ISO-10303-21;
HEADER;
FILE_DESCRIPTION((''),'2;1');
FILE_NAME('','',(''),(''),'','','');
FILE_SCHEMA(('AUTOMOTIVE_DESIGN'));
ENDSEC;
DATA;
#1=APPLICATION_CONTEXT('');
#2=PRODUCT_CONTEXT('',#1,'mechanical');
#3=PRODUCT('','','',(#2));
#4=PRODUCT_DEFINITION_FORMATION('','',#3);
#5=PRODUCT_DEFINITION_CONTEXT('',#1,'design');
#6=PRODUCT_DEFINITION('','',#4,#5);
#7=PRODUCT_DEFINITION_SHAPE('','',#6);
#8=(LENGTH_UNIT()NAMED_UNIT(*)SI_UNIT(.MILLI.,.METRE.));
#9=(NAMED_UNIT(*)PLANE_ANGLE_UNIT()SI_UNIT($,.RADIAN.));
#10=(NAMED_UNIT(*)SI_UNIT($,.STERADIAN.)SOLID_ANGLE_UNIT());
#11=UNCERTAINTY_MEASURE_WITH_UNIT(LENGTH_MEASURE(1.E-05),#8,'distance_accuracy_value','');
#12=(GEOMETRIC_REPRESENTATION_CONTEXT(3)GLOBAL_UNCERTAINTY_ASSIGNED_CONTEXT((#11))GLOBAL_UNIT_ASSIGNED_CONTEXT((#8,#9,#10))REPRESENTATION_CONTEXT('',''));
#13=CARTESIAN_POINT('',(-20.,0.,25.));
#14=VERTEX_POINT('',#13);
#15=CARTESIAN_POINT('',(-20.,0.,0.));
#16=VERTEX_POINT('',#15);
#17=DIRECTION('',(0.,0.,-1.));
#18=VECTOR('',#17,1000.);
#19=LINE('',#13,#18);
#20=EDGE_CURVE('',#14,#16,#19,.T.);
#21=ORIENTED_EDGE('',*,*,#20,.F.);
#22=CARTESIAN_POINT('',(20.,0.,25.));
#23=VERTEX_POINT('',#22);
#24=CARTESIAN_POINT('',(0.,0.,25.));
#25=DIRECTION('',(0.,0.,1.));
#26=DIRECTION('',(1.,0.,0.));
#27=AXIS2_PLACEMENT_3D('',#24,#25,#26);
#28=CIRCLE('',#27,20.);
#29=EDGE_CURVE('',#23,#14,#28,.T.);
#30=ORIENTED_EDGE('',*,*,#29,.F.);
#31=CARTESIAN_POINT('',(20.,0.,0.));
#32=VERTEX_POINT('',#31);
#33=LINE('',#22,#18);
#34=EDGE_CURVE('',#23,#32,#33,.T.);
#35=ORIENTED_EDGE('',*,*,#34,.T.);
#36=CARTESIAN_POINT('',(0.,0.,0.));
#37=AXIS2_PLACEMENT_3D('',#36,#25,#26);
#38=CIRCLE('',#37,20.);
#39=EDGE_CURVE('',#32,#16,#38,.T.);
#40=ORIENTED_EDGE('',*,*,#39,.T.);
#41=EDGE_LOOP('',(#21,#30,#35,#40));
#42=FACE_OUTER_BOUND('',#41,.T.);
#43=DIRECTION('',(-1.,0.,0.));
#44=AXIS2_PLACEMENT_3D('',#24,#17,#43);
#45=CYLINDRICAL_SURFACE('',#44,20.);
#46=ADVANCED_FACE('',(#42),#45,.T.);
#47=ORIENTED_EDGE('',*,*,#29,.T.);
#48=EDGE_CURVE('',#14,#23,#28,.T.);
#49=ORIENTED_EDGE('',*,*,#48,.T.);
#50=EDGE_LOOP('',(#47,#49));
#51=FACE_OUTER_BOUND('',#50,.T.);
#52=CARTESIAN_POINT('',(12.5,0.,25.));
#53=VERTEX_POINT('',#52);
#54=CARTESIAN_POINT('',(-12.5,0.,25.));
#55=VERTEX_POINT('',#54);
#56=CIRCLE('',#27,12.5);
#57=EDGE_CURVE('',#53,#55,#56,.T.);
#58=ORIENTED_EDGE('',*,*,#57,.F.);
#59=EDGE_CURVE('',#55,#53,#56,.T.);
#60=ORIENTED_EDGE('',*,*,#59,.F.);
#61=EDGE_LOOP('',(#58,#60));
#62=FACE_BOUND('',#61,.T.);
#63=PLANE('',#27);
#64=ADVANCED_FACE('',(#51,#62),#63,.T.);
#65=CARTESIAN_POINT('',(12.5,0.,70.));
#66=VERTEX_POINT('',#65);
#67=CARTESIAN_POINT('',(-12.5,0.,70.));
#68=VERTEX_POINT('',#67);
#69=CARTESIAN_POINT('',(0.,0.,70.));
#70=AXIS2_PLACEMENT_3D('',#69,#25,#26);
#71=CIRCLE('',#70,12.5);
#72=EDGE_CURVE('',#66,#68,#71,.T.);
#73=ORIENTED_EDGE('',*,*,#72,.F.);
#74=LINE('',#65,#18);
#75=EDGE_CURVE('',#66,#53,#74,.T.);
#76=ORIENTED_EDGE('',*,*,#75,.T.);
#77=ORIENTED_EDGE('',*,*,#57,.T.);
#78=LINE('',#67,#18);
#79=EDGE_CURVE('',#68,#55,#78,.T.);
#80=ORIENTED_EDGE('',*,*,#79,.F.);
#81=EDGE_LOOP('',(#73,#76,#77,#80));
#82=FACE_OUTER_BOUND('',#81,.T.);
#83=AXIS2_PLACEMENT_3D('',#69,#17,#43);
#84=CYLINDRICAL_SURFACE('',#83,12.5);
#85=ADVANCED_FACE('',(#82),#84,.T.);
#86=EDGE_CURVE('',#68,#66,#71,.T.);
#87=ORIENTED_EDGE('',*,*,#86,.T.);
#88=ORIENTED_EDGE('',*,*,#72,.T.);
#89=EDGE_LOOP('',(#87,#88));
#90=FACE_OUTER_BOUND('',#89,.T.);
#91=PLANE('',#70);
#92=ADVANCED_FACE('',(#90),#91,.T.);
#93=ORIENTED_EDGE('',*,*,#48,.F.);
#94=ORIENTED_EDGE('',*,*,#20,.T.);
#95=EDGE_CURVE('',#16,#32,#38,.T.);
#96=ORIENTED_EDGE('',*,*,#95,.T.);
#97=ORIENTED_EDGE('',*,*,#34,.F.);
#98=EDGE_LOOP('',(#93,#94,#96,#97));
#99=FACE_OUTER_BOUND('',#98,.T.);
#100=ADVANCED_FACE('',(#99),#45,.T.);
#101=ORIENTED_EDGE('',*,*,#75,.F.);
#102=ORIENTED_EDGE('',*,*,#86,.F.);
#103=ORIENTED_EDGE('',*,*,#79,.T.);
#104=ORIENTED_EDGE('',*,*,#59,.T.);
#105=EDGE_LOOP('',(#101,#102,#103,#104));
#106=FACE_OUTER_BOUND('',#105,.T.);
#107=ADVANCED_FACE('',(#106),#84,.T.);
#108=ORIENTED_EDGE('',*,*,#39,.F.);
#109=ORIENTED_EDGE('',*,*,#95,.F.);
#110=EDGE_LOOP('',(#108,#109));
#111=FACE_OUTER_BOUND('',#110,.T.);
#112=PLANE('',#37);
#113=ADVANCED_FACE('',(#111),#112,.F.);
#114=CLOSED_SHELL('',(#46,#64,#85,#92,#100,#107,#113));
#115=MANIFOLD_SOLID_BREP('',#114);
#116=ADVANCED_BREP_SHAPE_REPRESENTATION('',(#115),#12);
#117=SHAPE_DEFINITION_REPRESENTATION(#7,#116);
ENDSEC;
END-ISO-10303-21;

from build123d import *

# Parameters (mm, degrees)
SKETCH_1_R      = 20
EXTRUDE_1_DEPTH = 25
SKETCH_2_R      = 12.5
EXTRUDE_2_DEPTH = 45


with BuildPart() as part:
    # 草图1 → 凸台-拉伸1 (new body)
    with BuildSketch(Plane.XY):
        Circle(SKETCH_1_R)
    extrude(amount=EXTRUDE_1_DEPTH)

    # 草图2 → 凸台-拉伸2 (add)
    with BuildSketch(Plane.XY.offset(25)):
        with Locations(Location((0, 0, 0), (0, 0, 180))):
            Circle(SKETCH_2_R)
    extrude(amount=EXTRUDE_2_DEPTH)


solid = part.part
